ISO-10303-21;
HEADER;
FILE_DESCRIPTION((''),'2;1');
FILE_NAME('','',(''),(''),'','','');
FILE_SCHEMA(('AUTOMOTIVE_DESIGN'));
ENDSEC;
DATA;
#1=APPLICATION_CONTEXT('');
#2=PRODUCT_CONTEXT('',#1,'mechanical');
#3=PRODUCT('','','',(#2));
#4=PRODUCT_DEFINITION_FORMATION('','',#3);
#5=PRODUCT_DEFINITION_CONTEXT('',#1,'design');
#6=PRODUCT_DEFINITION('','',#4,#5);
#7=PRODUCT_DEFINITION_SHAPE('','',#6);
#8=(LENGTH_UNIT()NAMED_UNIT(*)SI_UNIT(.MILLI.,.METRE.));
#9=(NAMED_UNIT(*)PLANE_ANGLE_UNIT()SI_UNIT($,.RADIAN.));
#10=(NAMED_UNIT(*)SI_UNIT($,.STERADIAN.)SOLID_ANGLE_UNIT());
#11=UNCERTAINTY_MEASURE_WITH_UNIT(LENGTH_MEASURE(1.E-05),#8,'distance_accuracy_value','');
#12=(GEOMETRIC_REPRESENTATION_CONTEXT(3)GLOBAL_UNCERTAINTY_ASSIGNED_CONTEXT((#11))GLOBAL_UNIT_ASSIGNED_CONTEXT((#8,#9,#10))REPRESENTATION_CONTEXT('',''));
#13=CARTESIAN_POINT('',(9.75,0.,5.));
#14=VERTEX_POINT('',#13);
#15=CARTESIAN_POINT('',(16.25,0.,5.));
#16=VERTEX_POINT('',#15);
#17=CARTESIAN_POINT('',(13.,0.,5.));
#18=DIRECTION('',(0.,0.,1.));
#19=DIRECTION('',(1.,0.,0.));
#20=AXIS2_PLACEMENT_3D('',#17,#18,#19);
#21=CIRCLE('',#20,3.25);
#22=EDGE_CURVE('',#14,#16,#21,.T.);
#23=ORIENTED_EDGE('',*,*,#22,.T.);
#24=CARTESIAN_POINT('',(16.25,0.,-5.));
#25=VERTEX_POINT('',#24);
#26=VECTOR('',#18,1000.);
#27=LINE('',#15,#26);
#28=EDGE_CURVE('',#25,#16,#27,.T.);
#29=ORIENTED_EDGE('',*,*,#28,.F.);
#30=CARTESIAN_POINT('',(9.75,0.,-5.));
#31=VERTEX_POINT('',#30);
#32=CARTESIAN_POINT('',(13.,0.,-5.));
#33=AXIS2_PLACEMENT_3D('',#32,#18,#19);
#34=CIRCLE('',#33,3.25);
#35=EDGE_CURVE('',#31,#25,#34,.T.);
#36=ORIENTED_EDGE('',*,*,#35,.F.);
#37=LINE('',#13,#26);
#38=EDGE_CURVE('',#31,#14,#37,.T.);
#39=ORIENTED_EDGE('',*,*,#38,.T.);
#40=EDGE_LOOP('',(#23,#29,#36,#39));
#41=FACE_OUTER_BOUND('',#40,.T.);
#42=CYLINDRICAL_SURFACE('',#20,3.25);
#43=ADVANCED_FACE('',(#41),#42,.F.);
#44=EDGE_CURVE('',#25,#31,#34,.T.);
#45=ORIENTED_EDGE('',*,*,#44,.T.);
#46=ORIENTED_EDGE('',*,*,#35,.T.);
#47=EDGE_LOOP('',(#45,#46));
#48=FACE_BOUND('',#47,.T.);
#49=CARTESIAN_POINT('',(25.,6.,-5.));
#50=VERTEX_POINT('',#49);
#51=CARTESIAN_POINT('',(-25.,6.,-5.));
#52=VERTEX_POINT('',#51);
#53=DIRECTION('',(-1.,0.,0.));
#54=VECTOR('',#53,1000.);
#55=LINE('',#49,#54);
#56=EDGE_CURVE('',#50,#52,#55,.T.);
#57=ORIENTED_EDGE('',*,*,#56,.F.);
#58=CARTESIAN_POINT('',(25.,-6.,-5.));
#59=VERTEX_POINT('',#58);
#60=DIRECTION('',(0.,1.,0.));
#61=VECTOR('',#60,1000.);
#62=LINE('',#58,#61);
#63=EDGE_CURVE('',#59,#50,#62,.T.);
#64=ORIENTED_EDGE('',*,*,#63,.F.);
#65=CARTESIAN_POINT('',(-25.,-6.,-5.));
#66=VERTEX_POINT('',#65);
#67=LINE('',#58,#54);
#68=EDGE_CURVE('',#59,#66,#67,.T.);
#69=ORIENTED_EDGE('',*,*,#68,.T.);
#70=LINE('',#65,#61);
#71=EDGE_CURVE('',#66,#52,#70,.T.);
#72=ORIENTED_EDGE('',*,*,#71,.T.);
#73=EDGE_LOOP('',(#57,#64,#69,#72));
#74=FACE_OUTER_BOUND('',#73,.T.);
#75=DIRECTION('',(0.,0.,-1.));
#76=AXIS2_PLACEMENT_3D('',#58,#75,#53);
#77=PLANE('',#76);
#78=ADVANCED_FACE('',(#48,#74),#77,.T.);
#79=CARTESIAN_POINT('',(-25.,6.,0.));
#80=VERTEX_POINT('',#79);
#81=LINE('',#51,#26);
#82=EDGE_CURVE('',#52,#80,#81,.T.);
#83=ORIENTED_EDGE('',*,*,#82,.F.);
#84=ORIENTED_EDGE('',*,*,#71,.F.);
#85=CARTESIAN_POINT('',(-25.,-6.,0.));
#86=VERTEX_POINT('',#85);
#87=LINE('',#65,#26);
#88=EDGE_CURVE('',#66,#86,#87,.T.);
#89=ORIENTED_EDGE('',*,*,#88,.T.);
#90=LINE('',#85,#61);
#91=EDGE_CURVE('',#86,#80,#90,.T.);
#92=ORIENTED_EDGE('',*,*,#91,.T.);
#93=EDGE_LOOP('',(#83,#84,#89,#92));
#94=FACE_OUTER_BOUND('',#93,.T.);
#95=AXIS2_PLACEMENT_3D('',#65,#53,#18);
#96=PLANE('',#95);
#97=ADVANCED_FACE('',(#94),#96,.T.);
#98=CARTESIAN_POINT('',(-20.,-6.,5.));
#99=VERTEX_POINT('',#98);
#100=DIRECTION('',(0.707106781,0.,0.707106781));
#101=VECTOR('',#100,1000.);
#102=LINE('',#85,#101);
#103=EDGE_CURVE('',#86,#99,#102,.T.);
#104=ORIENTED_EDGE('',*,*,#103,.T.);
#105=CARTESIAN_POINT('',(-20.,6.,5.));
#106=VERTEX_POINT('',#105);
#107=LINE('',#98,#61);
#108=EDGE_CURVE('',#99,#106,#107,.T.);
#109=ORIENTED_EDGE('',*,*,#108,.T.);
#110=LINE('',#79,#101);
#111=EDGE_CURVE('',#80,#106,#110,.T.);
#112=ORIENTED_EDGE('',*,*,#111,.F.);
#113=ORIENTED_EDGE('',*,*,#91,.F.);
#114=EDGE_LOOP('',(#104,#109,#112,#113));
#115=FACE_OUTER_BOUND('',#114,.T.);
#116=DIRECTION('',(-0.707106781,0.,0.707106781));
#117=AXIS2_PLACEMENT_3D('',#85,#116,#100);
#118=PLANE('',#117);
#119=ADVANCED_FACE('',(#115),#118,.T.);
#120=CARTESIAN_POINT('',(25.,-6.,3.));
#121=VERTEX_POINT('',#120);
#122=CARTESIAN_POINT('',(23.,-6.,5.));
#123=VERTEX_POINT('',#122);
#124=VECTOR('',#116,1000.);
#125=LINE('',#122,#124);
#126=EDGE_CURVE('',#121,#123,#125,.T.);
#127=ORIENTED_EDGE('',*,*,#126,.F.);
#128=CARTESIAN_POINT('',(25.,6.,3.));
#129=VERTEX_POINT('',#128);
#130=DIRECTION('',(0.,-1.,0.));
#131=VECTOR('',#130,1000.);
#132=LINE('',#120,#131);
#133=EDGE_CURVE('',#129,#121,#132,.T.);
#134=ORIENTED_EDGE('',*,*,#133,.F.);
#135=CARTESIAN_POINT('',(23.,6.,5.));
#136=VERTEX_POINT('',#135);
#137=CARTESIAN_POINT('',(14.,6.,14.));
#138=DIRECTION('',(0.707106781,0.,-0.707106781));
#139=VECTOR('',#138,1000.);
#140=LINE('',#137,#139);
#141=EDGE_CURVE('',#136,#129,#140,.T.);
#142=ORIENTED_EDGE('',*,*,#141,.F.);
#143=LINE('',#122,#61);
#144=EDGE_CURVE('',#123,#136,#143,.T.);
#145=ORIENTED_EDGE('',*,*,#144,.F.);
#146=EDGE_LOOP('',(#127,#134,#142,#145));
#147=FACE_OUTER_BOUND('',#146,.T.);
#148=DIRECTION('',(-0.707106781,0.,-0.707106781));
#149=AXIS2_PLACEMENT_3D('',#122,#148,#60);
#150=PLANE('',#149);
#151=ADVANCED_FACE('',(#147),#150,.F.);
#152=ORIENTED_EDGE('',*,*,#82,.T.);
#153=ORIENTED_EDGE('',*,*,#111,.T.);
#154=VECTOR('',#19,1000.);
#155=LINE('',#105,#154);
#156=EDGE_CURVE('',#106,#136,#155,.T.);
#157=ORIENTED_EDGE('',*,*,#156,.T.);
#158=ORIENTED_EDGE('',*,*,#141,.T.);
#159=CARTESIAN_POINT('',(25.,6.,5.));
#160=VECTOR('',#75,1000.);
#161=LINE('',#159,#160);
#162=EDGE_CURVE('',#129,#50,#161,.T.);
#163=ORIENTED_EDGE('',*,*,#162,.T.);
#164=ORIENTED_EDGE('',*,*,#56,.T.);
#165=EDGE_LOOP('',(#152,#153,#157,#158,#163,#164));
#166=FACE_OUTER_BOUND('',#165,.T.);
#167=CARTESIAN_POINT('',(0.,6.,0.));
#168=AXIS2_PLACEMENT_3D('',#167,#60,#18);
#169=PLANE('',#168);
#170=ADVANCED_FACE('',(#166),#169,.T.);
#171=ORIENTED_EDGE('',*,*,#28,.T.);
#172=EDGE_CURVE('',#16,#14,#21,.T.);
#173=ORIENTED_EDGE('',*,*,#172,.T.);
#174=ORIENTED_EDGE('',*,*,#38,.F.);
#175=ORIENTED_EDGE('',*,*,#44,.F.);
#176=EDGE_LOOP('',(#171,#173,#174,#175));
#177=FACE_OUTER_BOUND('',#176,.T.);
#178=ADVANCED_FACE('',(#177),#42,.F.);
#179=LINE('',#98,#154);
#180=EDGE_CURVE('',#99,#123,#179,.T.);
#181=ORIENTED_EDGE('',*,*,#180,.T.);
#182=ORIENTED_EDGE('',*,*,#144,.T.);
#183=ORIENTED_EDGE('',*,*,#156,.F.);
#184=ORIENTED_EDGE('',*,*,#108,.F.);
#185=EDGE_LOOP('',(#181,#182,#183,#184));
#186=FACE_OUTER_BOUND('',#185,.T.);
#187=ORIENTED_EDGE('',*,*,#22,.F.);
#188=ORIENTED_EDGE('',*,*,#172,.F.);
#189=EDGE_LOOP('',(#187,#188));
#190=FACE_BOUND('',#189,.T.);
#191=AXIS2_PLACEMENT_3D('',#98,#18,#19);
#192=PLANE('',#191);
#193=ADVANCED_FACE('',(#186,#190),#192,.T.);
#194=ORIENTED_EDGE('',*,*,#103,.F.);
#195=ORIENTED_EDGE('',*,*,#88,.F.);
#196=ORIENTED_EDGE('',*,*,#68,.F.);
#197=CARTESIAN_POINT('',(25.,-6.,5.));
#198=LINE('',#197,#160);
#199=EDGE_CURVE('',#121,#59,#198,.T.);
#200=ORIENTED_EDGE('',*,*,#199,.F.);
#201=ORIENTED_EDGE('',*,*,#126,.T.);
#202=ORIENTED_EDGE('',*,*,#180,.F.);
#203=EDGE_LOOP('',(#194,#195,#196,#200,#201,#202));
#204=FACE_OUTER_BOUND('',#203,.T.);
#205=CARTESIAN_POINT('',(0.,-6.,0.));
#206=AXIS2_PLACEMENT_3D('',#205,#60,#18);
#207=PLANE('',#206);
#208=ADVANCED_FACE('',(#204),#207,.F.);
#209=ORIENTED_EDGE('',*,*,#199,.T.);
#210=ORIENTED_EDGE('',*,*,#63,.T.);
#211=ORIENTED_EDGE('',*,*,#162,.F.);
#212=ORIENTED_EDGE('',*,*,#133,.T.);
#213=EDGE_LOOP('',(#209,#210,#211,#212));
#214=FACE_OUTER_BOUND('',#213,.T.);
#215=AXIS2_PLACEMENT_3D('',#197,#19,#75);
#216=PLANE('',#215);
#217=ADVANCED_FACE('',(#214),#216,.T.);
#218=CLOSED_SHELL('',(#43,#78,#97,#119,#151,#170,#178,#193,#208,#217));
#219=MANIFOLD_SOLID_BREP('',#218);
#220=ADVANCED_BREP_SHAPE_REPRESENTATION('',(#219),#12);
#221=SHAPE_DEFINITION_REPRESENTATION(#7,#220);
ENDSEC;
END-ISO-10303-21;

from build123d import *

# Parameters (mm, degrees)
BOSS_EXTRUDE1_DEPTH        = 12
F_6_5_6_5_DIAMETER_HOLE1_D = 6.5
CHAMFER1_SIZE              = 2


with BuildPart() as part:
    # Sketch1 → Boss-Extrude1 (new body)
    with BuildSketch(Plane(origin=(0, 6, 0), x_dir=(1, 0, 0), z_dir=(0, 1, 0))):
        Polygon((-20, -5), (25, -5), (25, 5), (-25, 5), (-25, 0), align=None)
    extrude(amount=-BOSS_EXTRUDE1_DEPTH)

    # Ø6.5 (6.5) Diameter Hole1 (through all)
    with Locations(Plane.XY.offset(5)):
        with Locations((13, 0)):
            Hole(F_6_5_6_5_DIAMETER_HOLE1_D / 2)

    # Chamfer1
    chamfer1_edges = [part.edges().sort_by_distance(p)[0] for p in [
        (25, 0, 5),
    ]]
    chamfer(chamfer1_edges, length=CHAMFER1_SIZE)


solid = part.part
